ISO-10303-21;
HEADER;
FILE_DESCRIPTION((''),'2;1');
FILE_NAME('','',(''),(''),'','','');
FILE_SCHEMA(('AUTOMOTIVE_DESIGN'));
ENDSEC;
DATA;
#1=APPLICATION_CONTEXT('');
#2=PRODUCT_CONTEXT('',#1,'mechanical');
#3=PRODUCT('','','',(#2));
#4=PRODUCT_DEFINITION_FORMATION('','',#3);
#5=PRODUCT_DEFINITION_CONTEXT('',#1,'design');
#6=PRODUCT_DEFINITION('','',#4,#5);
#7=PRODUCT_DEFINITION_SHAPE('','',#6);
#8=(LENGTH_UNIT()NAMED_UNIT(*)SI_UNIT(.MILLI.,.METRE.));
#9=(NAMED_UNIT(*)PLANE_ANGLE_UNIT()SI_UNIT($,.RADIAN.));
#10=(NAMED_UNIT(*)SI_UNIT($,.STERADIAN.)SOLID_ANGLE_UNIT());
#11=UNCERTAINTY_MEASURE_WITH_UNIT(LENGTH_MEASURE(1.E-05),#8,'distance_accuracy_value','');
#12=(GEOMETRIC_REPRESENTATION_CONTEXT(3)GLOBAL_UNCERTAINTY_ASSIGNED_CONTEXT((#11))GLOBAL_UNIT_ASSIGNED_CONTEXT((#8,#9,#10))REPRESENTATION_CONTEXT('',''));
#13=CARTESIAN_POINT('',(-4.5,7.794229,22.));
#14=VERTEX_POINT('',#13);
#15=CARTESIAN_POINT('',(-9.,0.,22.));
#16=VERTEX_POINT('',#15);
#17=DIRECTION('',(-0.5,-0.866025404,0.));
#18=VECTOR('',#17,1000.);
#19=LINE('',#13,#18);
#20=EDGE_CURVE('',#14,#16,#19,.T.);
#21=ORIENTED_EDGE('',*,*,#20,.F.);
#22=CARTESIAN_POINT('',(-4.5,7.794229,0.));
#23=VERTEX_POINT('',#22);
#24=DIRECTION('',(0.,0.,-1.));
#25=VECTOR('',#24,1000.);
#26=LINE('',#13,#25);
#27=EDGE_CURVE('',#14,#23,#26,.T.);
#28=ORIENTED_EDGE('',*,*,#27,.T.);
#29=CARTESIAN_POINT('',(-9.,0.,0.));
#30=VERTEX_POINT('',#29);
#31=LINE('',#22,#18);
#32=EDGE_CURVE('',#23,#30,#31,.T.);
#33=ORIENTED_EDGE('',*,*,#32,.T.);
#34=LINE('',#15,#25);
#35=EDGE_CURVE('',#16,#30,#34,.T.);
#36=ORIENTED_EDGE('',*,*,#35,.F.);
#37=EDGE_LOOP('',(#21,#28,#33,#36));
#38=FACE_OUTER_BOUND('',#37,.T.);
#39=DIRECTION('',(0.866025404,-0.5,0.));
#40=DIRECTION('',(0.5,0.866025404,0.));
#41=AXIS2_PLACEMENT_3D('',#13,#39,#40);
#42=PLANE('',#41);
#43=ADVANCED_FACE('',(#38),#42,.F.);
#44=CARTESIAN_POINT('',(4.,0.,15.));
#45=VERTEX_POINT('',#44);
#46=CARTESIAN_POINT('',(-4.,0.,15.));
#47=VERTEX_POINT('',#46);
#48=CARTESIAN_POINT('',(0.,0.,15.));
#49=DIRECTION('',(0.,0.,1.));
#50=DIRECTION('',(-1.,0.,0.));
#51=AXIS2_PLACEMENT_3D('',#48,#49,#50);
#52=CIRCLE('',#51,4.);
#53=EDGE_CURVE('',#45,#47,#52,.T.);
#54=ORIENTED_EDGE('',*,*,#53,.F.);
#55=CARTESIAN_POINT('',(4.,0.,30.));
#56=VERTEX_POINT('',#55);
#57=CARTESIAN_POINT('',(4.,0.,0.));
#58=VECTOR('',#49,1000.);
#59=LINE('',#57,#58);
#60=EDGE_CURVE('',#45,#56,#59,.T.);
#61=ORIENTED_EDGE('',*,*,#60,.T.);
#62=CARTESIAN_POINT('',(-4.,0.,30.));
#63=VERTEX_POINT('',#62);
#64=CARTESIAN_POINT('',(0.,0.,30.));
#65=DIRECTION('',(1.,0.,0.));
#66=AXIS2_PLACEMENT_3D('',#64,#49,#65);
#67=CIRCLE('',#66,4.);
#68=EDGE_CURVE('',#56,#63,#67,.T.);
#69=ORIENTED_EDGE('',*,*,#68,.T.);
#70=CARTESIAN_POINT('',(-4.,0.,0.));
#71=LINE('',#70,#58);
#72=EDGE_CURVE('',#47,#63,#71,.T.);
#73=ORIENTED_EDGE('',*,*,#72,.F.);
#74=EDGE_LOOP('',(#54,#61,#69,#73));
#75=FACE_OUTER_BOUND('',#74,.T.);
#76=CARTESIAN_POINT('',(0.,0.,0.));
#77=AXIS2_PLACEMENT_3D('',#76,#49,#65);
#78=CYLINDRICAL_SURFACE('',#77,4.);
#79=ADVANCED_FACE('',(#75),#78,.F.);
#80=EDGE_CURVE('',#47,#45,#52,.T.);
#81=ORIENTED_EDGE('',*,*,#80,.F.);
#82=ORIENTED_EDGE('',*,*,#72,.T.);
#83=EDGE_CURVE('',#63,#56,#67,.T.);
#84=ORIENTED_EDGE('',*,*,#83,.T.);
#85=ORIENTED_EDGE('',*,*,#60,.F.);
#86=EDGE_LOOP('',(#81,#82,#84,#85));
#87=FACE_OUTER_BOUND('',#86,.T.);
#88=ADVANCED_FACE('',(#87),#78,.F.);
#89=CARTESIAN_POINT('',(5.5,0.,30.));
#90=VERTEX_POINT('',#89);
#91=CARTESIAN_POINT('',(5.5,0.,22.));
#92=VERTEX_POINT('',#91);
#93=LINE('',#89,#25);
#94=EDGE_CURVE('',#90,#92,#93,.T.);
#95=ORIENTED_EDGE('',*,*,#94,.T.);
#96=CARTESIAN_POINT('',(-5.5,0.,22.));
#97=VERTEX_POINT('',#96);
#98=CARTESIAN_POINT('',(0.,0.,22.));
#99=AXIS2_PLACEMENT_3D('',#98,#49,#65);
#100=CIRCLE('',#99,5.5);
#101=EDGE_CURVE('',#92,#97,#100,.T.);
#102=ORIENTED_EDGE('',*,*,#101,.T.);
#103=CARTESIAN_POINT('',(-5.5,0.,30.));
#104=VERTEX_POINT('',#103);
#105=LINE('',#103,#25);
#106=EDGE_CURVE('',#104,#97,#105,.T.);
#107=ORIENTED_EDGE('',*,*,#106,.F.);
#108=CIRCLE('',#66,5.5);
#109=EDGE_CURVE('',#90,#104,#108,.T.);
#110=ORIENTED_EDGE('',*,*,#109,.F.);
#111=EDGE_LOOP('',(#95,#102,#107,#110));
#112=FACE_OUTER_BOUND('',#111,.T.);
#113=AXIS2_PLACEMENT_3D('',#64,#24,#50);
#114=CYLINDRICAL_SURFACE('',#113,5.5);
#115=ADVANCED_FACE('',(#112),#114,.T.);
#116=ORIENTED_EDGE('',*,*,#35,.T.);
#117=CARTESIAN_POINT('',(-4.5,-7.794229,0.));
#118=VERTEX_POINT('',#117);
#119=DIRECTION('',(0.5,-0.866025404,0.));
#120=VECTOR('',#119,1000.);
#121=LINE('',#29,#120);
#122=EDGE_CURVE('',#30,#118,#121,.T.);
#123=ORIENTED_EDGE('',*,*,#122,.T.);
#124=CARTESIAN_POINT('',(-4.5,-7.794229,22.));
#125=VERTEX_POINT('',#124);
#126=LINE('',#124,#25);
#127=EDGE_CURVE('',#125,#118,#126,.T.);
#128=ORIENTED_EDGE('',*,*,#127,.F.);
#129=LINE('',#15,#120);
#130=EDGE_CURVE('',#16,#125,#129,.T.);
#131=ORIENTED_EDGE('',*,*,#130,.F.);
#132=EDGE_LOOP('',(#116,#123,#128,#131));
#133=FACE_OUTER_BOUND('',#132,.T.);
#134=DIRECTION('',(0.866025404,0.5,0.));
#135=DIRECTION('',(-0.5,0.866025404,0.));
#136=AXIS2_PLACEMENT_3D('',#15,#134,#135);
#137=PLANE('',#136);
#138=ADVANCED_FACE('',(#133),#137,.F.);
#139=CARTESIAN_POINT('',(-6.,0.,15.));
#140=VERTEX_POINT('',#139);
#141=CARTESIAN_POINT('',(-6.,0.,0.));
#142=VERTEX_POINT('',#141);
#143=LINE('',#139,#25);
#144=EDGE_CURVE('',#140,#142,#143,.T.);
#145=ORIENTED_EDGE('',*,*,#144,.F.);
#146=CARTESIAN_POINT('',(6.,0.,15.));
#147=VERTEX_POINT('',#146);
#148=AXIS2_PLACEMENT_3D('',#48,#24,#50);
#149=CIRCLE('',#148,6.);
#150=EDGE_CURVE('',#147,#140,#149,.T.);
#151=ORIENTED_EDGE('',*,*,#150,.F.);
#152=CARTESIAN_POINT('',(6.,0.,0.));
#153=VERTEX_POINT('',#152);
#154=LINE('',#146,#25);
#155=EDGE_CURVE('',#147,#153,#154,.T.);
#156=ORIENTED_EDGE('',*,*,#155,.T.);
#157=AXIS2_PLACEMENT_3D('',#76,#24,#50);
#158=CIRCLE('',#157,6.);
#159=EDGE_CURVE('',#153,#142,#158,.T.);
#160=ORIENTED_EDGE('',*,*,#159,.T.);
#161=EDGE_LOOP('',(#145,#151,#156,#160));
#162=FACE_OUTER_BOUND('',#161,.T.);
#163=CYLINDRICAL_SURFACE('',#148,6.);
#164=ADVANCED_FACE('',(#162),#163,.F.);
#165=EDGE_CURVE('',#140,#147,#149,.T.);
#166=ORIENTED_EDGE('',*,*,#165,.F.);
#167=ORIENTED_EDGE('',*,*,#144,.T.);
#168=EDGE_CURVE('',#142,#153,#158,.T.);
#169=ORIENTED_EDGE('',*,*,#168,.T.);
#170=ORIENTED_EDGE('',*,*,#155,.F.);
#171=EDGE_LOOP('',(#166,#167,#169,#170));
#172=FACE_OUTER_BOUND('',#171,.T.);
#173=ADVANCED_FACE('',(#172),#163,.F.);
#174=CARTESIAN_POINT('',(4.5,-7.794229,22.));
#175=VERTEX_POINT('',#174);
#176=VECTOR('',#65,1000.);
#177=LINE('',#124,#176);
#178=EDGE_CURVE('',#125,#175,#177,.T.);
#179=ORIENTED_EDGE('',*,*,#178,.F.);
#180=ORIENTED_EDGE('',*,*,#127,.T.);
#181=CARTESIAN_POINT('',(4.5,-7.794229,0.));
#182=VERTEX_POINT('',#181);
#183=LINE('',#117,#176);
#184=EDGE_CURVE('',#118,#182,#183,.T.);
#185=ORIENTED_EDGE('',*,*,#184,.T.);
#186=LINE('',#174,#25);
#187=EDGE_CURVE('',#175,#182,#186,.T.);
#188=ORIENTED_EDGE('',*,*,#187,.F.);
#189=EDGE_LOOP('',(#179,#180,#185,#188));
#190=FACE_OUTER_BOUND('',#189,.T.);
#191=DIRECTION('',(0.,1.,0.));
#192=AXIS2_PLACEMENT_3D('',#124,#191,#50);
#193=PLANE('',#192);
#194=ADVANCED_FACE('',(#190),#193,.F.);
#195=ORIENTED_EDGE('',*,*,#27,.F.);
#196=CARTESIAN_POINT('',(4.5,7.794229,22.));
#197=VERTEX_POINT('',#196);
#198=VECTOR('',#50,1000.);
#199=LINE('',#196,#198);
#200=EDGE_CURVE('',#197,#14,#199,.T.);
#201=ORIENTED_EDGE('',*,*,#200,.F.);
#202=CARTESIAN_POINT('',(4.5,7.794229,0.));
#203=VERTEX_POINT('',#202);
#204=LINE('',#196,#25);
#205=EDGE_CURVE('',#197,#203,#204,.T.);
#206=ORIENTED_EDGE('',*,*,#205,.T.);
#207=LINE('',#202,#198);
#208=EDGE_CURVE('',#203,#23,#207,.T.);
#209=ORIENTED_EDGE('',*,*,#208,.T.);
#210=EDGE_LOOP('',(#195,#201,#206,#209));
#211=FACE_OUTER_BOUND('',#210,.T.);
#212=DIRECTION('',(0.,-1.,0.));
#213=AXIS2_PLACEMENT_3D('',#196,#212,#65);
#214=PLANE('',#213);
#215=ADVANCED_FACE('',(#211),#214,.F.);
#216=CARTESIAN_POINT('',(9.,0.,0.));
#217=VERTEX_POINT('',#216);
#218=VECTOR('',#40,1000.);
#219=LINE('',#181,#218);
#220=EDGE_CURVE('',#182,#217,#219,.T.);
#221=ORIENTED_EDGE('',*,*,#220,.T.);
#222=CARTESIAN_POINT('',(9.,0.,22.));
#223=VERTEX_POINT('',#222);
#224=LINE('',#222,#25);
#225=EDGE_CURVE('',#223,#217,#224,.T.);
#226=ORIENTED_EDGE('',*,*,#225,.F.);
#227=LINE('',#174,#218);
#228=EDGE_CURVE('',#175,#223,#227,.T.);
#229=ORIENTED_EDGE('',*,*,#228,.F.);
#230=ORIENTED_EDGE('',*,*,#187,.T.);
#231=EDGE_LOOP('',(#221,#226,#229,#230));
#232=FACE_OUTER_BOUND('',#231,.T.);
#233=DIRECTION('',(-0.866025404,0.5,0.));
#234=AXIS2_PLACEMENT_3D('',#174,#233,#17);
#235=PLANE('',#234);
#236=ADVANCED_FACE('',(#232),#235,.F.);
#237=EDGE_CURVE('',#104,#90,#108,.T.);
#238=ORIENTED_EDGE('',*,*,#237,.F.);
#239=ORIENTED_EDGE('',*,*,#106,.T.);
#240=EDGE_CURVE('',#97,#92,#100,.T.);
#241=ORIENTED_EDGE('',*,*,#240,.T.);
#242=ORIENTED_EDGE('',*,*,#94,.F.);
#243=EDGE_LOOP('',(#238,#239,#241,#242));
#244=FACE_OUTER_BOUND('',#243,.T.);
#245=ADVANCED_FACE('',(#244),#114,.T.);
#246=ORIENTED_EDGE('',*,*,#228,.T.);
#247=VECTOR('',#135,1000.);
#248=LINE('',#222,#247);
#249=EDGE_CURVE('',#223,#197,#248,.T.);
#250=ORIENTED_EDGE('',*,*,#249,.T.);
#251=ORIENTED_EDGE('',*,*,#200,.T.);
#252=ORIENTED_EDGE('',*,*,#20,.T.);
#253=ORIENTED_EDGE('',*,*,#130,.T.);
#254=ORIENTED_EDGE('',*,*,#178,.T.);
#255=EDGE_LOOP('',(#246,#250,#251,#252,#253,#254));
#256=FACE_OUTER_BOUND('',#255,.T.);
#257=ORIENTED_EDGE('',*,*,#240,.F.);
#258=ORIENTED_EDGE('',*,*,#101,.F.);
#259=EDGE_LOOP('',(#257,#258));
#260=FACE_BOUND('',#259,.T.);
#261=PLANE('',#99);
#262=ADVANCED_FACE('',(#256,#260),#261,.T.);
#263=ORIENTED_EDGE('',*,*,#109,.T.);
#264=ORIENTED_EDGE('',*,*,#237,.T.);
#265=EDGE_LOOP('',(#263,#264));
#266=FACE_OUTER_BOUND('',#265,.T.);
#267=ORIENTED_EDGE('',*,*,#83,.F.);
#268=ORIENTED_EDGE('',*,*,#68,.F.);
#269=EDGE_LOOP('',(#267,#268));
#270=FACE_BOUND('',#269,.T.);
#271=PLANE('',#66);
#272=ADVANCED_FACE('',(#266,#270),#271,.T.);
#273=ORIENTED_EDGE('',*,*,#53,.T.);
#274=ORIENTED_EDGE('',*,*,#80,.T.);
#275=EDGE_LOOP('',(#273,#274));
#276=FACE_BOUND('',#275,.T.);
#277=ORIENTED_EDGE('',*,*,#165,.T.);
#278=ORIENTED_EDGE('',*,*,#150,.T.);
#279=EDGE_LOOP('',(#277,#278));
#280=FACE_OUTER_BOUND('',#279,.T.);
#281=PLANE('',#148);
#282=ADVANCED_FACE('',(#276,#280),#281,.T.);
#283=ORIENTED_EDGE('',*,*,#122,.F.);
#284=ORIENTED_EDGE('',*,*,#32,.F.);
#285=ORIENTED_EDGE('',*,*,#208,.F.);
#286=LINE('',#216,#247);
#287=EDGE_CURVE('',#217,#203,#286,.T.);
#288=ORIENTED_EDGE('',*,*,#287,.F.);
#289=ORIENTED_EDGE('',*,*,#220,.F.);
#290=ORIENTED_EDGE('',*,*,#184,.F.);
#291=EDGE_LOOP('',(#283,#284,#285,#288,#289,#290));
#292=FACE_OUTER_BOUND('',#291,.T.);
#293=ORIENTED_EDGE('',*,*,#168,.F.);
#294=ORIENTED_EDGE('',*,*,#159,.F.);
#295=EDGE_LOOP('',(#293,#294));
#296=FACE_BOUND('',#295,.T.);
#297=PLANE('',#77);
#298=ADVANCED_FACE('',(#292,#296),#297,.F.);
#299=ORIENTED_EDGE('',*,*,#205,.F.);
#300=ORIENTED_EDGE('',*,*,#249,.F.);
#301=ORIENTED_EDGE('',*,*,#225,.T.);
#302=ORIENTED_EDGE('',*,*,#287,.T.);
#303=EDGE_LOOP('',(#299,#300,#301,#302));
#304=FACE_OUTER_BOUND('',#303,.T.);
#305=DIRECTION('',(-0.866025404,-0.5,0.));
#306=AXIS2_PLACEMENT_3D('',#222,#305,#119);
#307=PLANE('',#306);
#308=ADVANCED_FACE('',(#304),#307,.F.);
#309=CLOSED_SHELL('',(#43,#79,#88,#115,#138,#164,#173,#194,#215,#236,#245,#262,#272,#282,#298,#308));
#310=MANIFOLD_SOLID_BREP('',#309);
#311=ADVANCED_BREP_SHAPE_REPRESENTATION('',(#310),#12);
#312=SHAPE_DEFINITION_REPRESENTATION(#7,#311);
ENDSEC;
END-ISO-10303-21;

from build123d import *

# Parameters (mm, degrees)
HEX_BODY_22MM_DEPTH       = 22
SPIGOT_SKETCH_11_R        = 5.5
SPIGOT_11X8_DEPTH         = 8
SPIGOT_BORE_SKETCH_R      = 4
SPIGOT_THROUGH_BORE_DEPTH = 33.276152187
HEX_BORE_SKETCH_12_R      = 6
HEX_BORE_12X15_DEPTH      = 15


with BuildPart() as part:
    # Hex Profile Sketch → Hex Body 22mm (new body)
    with BuildSketch(Plane.XY):
        Polygon((9, 0), (4.5, 7.794228634), (-4.5, 7.794228634), (-9, 0), (-4.5, -7.794228634), (4.5, -7.794228634), align=None)
    extrude(amount=HEX_BODY_22MM_DEPTH)

    # Spigot Sketch Ø11 → Spigot Ø11x8 (add)
    with BuildSketch(Plane.XY.offset(22)):
        Circle(SPIGOT_SKETCH_11_R)
    extrude(amount=SPIGOT_11X8_DEPTH)

    # Spigot Bore Sketch → Spigot Through Bore (cut, through all)
    with BuildSketch(Plane.XY.offset(30)):
        Circle(SPIGOT_BORE_SKETCH_R)
    extrude(amount=-SPIGOT_THROUGH_BORE_DEPTH, mode=Mode.SUBTRACT)

    # Hex Bore Sketch Ø12 → Hex Bore Ø12x15 (cut)
    with BuildSketch(Plane(origin=(0, 0, 0), x_dir=(-1, 0, 0), z_dir=(0, 0, -1))):
        Circle(HEX_BORE_SKETCH_12_R)
    extrude(amount=-HEX_BORE_12X15_DEPTH, mode=Mode.SUBTRACT)


solid = part.part
